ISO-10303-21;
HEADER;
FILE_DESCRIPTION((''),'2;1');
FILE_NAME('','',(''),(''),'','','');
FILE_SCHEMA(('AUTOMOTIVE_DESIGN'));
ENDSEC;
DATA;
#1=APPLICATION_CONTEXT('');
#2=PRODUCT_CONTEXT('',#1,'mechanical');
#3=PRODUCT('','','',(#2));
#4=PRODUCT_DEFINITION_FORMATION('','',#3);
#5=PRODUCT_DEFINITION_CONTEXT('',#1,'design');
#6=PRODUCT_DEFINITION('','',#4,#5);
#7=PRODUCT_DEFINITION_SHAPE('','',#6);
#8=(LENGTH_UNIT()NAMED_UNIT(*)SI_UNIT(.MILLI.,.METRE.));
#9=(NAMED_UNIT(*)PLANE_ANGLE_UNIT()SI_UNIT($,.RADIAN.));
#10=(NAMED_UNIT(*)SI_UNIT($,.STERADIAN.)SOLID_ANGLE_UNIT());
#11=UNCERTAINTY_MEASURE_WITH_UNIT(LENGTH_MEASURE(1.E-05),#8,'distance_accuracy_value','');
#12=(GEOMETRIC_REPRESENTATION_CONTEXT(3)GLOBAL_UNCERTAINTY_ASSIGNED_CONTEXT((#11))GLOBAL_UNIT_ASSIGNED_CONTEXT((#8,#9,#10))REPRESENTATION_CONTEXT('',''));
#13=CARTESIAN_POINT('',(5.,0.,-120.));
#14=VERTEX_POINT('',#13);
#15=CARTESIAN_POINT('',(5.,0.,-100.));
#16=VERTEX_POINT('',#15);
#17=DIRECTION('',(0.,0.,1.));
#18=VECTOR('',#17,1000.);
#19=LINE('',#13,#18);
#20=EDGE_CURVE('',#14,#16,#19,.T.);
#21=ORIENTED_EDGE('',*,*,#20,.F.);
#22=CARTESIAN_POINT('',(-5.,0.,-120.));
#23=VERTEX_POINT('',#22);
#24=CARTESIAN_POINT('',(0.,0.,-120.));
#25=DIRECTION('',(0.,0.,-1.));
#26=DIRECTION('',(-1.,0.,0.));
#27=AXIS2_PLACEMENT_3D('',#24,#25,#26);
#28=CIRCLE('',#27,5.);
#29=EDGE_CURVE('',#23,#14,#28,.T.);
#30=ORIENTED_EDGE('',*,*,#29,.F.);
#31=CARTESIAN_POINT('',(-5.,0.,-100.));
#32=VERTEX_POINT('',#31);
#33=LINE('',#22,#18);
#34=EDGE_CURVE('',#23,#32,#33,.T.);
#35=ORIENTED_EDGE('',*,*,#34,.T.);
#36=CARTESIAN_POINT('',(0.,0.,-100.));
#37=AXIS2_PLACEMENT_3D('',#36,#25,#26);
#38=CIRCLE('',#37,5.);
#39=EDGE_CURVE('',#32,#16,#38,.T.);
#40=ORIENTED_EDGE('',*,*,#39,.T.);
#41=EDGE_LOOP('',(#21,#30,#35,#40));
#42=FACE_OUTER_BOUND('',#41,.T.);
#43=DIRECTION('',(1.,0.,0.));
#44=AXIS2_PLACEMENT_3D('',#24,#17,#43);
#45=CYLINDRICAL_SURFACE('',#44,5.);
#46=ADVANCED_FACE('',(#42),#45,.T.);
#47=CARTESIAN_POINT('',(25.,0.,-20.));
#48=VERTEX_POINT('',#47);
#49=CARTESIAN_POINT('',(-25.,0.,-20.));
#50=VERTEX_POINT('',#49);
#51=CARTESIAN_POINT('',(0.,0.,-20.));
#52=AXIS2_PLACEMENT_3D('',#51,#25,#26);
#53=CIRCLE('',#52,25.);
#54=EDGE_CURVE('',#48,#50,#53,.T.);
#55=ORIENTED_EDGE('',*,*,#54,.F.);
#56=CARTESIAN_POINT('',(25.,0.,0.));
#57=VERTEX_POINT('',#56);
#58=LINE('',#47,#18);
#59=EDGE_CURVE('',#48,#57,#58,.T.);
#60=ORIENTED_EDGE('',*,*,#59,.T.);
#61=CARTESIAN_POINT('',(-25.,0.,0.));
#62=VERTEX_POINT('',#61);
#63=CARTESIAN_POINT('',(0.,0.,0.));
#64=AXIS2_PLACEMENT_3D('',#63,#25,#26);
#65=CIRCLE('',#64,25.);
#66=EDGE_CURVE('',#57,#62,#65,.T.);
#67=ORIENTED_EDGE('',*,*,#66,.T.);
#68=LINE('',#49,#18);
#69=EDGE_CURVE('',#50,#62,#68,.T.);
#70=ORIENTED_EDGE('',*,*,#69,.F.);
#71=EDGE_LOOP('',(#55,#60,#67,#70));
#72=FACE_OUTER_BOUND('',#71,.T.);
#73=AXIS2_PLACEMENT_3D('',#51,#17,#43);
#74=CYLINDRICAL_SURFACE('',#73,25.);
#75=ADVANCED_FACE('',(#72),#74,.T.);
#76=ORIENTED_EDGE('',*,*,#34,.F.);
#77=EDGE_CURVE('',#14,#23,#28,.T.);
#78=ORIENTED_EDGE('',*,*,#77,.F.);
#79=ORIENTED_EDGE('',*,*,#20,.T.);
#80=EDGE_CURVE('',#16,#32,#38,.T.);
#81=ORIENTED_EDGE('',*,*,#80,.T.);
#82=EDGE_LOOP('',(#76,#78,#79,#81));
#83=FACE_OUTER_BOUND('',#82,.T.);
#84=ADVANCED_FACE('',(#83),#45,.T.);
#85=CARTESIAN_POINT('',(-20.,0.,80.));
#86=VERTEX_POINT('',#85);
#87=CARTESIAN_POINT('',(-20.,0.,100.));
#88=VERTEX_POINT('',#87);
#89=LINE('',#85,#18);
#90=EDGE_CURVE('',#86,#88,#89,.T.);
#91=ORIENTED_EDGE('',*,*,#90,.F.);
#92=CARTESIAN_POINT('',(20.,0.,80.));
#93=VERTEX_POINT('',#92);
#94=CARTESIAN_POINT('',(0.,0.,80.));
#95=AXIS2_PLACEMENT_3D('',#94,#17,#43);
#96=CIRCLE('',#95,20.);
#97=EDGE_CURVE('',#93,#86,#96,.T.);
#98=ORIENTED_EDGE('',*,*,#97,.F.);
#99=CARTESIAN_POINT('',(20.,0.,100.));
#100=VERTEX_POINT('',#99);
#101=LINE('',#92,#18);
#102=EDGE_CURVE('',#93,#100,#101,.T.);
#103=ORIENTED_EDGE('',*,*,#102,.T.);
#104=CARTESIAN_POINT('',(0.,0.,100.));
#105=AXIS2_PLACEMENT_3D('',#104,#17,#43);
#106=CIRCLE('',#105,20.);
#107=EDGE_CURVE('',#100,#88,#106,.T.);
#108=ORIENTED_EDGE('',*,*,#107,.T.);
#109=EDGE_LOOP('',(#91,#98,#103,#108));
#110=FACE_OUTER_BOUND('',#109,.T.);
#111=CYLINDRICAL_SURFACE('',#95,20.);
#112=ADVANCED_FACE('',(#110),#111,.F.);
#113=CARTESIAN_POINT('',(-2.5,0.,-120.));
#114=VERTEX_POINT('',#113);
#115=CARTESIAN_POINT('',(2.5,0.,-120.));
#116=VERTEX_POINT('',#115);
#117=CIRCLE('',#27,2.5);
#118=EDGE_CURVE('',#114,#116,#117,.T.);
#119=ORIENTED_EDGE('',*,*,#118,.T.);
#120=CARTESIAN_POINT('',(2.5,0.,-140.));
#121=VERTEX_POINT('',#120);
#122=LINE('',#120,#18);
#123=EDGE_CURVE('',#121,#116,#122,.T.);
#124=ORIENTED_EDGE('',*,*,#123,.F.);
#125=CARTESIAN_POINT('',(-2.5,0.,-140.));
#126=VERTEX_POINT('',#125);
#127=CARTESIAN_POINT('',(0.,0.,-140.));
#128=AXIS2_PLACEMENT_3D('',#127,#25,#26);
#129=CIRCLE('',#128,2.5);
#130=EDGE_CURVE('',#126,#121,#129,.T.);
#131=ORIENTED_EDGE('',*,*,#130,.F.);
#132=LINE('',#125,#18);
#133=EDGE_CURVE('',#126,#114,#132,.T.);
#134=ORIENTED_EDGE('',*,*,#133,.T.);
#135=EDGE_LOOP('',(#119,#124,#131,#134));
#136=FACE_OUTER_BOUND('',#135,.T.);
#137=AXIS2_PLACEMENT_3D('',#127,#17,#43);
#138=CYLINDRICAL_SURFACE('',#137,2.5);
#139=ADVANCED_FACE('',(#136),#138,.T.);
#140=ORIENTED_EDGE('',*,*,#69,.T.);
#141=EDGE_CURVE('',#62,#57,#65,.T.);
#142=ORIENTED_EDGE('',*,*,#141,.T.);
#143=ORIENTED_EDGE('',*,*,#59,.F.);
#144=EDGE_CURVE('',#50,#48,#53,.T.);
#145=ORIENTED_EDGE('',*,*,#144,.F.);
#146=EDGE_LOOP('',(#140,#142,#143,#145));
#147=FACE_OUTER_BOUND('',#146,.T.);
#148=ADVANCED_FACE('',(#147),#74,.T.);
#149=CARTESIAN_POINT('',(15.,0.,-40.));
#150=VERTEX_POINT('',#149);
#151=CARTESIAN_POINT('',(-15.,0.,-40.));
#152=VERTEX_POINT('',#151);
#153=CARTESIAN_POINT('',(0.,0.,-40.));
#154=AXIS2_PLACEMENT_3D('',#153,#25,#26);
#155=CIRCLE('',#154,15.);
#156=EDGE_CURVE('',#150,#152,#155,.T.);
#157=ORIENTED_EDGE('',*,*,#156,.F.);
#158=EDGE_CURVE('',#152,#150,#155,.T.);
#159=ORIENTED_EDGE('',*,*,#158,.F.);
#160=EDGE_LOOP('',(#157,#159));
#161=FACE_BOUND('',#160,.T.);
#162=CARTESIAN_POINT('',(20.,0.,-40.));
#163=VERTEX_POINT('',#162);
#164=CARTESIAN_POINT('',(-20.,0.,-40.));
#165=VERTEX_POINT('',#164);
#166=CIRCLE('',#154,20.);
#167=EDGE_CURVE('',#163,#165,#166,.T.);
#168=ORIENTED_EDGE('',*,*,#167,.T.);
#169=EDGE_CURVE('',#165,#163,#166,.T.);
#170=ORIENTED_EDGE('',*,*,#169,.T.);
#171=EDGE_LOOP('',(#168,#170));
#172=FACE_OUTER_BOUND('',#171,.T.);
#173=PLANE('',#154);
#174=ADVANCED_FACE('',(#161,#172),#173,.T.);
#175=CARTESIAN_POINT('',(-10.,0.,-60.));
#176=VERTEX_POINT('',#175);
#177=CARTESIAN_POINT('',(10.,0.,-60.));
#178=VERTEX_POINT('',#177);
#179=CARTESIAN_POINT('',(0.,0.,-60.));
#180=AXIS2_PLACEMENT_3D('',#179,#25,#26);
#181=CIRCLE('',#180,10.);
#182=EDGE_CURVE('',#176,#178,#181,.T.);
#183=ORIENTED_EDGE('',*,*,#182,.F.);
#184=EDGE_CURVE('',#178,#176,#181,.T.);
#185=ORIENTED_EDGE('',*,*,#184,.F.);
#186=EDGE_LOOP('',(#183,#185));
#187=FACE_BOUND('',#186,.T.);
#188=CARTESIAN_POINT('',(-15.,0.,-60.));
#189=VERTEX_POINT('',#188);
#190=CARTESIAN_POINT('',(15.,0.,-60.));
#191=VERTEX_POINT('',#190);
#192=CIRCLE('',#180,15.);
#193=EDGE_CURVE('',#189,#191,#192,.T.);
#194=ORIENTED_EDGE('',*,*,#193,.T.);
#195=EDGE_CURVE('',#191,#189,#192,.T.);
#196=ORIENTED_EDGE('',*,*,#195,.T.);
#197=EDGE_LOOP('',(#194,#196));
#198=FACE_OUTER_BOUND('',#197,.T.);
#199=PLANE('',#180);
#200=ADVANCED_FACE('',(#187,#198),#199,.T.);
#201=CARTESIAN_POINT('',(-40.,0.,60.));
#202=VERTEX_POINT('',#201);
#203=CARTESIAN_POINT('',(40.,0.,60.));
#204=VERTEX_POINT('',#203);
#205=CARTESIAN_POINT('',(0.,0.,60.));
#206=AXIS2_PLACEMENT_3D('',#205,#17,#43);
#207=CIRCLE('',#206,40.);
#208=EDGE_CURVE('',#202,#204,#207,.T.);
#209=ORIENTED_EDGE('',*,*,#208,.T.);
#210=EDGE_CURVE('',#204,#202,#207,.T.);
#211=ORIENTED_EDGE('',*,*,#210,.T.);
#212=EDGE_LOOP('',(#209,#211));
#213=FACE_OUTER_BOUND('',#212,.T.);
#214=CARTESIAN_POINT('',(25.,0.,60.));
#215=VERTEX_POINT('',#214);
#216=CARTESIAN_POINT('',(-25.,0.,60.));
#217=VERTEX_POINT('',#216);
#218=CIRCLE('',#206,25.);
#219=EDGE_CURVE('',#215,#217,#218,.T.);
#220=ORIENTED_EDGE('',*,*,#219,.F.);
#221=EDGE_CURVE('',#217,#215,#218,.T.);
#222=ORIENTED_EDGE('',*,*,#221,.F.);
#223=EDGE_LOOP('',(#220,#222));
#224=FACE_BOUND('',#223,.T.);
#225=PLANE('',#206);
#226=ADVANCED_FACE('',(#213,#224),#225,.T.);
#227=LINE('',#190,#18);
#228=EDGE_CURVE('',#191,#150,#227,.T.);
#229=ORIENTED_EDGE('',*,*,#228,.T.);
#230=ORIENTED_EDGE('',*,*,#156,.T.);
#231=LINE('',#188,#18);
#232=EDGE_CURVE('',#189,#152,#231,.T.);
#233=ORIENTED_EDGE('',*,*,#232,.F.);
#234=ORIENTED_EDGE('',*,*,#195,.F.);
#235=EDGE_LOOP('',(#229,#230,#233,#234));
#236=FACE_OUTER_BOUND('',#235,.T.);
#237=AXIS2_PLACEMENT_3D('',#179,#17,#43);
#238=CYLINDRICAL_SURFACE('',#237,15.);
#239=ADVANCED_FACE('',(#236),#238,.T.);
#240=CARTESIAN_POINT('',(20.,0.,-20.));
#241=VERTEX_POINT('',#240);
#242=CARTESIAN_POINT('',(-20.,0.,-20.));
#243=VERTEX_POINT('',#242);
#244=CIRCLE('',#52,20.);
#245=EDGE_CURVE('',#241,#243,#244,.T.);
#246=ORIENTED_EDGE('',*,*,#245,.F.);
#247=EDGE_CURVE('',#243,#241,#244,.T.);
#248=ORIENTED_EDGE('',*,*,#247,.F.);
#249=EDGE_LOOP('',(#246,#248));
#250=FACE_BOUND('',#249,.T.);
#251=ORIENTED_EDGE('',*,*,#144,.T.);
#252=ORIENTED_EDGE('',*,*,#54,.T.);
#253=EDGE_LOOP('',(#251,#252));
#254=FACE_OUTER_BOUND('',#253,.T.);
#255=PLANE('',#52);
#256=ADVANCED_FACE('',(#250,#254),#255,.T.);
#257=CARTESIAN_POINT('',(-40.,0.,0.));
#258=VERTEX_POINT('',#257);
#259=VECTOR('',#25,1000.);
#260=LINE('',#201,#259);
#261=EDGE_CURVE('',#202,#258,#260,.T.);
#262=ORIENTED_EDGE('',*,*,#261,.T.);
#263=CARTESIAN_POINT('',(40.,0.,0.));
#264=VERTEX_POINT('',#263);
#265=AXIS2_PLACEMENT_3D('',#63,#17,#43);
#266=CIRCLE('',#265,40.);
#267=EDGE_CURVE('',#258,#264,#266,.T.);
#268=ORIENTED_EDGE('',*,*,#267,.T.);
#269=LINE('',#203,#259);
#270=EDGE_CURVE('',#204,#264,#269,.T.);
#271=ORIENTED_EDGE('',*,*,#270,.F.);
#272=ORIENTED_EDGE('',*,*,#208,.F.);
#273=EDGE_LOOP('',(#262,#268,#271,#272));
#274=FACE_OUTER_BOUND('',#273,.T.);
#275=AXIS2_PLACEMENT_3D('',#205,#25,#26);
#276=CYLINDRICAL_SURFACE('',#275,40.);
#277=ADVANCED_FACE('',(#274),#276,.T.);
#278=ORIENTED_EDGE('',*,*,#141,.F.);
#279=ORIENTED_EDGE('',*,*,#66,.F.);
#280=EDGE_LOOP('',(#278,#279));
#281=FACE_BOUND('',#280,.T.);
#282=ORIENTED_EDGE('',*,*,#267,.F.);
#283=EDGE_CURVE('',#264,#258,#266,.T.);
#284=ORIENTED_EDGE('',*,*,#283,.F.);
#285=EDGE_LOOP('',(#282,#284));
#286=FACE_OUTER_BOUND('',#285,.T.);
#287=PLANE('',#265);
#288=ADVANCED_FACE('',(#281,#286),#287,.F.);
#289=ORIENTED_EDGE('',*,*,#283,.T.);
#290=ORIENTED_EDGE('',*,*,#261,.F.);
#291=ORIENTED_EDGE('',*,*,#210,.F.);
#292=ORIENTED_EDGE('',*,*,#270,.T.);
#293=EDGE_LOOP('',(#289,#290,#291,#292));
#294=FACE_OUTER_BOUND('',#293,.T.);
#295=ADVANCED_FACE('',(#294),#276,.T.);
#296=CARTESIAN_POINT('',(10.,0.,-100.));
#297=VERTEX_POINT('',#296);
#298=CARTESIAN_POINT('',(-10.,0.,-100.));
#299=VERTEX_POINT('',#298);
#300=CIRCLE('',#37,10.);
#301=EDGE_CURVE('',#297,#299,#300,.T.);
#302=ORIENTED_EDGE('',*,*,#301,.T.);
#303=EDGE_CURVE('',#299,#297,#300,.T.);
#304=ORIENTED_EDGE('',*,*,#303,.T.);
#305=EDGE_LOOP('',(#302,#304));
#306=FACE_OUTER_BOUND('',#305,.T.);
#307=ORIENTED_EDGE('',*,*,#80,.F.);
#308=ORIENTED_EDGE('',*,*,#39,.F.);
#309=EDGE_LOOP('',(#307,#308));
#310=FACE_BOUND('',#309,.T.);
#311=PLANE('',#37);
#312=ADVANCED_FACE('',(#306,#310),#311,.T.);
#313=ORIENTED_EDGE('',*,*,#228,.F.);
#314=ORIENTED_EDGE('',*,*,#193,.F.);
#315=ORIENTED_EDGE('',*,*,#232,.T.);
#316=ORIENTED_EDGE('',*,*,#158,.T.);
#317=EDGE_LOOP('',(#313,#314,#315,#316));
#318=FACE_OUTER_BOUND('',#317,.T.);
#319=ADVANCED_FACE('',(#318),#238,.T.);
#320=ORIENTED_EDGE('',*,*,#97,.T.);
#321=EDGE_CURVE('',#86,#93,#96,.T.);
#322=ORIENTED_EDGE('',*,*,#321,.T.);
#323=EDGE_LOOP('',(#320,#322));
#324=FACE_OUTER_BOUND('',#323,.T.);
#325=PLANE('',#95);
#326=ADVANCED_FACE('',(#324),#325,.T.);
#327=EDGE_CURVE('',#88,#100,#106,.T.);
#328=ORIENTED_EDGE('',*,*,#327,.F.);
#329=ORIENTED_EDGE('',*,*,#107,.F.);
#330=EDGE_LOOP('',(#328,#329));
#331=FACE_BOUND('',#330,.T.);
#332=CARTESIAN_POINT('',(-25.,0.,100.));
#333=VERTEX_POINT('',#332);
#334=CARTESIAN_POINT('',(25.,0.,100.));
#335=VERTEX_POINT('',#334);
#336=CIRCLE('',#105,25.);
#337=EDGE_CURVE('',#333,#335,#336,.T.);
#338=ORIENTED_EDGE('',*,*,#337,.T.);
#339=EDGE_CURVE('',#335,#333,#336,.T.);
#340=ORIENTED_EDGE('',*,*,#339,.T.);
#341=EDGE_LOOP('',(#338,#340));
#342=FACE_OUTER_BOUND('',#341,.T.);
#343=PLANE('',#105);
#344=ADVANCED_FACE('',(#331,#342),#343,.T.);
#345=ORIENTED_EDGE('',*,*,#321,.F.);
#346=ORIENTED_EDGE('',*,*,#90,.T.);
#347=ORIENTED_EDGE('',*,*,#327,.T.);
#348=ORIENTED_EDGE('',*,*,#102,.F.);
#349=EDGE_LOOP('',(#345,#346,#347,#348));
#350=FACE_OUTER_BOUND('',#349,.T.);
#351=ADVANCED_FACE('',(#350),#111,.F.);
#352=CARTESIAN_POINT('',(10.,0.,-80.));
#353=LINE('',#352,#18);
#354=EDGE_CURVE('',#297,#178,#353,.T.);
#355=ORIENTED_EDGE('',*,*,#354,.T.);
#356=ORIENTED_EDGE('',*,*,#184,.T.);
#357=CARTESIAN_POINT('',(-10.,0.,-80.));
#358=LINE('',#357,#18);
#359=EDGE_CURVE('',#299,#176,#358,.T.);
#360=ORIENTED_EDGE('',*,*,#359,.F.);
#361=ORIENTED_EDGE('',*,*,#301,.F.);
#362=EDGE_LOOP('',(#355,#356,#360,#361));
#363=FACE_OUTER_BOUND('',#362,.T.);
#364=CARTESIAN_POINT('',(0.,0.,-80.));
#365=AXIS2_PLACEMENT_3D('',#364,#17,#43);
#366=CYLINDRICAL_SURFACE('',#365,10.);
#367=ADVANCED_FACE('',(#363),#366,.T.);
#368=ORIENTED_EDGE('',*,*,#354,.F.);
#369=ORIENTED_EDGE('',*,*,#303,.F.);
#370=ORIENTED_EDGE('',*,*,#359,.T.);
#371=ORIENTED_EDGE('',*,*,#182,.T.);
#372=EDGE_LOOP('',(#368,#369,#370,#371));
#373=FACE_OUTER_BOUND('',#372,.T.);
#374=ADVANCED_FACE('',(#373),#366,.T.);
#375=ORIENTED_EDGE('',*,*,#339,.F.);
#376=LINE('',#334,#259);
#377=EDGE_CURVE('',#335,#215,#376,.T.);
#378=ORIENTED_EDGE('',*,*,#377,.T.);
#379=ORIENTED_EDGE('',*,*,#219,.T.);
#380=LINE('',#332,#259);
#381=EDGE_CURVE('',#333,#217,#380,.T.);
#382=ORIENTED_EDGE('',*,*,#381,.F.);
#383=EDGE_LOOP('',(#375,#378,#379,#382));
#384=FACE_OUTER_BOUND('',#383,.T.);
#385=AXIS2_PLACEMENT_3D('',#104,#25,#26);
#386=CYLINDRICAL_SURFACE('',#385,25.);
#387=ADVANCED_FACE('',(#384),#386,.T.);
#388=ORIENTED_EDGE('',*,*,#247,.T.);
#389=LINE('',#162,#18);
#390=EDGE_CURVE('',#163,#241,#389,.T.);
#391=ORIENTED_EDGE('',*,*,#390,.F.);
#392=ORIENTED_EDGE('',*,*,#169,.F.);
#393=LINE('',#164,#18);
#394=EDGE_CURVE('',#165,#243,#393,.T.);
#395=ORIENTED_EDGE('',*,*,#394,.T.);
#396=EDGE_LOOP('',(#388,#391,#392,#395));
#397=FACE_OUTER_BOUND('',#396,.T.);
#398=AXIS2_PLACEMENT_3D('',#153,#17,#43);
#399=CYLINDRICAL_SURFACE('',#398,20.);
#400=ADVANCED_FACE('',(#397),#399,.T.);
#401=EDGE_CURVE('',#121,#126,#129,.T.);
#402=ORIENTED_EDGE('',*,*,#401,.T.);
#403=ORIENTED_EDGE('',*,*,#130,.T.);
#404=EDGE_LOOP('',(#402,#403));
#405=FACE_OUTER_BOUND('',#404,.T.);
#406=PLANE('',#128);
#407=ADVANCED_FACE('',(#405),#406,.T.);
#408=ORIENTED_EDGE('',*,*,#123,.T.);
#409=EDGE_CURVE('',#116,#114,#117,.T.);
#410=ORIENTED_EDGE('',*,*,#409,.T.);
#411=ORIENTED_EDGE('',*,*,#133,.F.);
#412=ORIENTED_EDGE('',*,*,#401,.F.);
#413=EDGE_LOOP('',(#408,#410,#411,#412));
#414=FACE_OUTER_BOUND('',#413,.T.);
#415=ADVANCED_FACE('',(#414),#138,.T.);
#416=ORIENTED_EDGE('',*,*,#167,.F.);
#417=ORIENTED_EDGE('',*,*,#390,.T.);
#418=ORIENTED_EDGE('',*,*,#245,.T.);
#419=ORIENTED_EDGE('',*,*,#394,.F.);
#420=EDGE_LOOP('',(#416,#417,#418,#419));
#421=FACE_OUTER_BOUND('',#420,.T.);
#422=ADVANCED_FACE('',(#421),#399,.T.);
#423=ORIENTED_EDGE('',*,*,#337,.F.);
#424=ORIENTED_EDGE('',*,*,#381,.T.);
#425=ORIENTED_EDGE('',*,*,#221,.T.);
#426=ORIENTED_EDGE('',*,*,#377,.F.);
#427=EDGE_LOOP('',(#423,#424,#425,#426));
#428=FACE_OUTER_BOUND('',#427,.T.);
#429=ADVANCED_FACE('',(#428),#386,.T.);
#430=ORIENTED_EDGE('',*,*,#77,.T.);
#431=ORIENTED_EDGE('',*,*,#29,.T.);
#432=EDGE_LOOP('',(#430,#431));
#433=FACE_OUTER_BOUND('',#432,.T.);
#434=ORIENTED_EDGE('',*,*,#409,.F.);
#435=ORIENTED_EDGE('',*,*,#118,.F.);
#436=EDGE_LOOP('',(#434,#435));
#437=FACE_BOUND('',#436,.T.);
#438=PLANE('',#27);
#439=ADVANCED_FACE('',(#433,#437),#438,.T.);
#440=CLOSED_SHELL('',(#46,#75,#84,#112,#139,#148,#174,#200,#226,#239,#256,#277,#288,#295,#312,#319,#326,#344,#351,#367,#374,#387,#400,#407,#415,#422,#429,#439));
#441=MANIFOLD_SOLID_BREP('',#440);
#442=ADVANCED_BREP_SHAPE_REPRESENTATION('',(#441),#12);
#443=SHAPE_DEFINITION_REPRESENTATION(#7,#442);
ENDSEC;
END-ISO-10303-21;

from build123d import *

# Parameters (mm, degrees)
COLLAR_PROFILE_80_R     = 40
COLLAR_80_DEPTH         = 60
SPIGOT_SKETCH_50_R      = 25
SPIGOT_50_DEPTH         = 40
SPIGOT_BORE_SKETCH_40_R = 20
SPIGOT_BORE_40_DEPTH    = 20
PIN_START               = 20
PIN_STEP_1_SKETCH_50_R  = 25
PIN_STEP_1_50_DEPTH     = 20
PIN_STEP_2_SKETCH_40_R  = 20
PIN_STEP_2_40_DEPTH     = 20
PIN_STEP_3_SKETCH_30_R  = 15
PIN_STEP_3_30_DEPTH     = 20
PIN_STEP_4_SKETCH_20_R  = 10
PIN_STEP_4_20_DEPTH     = 20
PIN_STEP_5_SKETCH_20_R  = 10
PIN_STEP_5_20_DEPTH     = 20
PIN_STEP_6_SKETCH_10_R  = 5
PIN_STEP_6_10_DEPTH     = 20
PIN_TIP_SKETCH_5_R      = 2.5
PIN_TIP_5_DEPTH         = 20


with BuildPart() as part:
    # Collar Profile Ø80 → Collar Ø80 (new body)
    with BuildSketch(Plane.XY):
        Circle(COLLAR_PROFILE_80_R)
    extrude(amount=COLLAR_80_DEPTH)

    # Spigot Sketch Ø50 → Spigot Ø50 (add)
    with BuildSketch(Plane.XY.offset(60)):
        Circle(SPIGOT_SKETCH_50_R)
    extrude(amount=SPIGOT_50_DEPTH)

    # Spigot Bore Sketch Ø40 → Spigot Bore Ø40 (cut)
    with BuildSketch(Plane.XY.offset(100)):
        Circle(SPIGOT_BORE_SKETCH_40_R)
    extrude(amount=-SPIGOT_BORE_40_DEPTH, mode=Mode.SUBTRACT)

    # Pin Step 1 Sketch Ø50 → Pin Step 1 Ø50 (add)
    with BuildSketch(Plane(origin=(0, 0, 0), x_dir=(-1, 0, 0), z_dir=(0, 0, -1)).offset(PIN_START)):
        with Locations(Location((0, 0, 0), (0, 0, 180))):
            Circle(PIN_STEP_1_SKETCH_50_R)
    extrude(amount=-PIN_STEP_1_50_DEPTH)

    # Pin Step 2 Sketch Ø40 → Pin Step 2 Ø40 (add)
    with BuildSketch(Plane(origin=(0, 0, -20), x_dir=(-1, 0, 0), z_dir=(0, 0, -1))):
        with Locations(Location((0, 0, 0), (0, 0, 180))):
            Circle(PIN_STEP_2_SKETCH_40_R)
    extrude(amount=PIN_STEP_2_40_DEPTH)

    # Pin Step 3 Sketch Ø30 → Pin Step 3 Ø30 (add)
    with BuildSketch(Plane(origin=(0, 0, -40), x_dir=(-1, 0, 0), z_dir=(0, 0, -1))):
        Circle(PIN_STEP_3_SKETCH_30_R)
    extrude(amount=PIN_STEP_3_30_DEPTH)

    # Pin Step 4 Sketch Ø20 → Pin Step 4 Ø20 (add)
    with BuildSketch(Plane(origin=(0, 0, -60), x_dir=(-1, 0, 0), z_dir=(0, 0, -1))):
        Circle(PIN_STEP_4_SKETCH_20_R)
    extrude(amount=PIN_STEP_4_20_DEPTH)

    # Pin Step 5 Sketch Ø20 → Pin Step 5 Ø20 (add)
    with BuildSketch(Plane(origin=(0, 0, -80), x_dir=(-1, 0, 0), z_dir=(0, 0, -1))):
        Circle(PIN_STEP_5_SKETCH_20_R)
    extrude(amount=PIN_STEP_5_20_DEPTH)

    # Pin Step 6 Sketch Ø10 → Pin Step 6 Ø10 (add)
    with BuildSketch(Plane(origin=(0, 0, -100), x_dir=(-1, 0, 0), z_dir=(0, 0, -1))):
        Circle(PIN_STEP_6_SKETCH_10_R)
    extrude(amount=PIN_STEP_6_10_DEPTH)

    # Pin Tip Sketch Ø5 → Pin Tip Ø5 (add)
    with BuildSketch(Plane(origin=(0, 0, -120), x_dir=(-1, 0, 0), z_dir=(0, 0, -1))):
        Circle(PIN_TIP_SKETCH_5_R)
    extrude(amount=PIN_TIP_5_DEPTH)


solid = part.part
